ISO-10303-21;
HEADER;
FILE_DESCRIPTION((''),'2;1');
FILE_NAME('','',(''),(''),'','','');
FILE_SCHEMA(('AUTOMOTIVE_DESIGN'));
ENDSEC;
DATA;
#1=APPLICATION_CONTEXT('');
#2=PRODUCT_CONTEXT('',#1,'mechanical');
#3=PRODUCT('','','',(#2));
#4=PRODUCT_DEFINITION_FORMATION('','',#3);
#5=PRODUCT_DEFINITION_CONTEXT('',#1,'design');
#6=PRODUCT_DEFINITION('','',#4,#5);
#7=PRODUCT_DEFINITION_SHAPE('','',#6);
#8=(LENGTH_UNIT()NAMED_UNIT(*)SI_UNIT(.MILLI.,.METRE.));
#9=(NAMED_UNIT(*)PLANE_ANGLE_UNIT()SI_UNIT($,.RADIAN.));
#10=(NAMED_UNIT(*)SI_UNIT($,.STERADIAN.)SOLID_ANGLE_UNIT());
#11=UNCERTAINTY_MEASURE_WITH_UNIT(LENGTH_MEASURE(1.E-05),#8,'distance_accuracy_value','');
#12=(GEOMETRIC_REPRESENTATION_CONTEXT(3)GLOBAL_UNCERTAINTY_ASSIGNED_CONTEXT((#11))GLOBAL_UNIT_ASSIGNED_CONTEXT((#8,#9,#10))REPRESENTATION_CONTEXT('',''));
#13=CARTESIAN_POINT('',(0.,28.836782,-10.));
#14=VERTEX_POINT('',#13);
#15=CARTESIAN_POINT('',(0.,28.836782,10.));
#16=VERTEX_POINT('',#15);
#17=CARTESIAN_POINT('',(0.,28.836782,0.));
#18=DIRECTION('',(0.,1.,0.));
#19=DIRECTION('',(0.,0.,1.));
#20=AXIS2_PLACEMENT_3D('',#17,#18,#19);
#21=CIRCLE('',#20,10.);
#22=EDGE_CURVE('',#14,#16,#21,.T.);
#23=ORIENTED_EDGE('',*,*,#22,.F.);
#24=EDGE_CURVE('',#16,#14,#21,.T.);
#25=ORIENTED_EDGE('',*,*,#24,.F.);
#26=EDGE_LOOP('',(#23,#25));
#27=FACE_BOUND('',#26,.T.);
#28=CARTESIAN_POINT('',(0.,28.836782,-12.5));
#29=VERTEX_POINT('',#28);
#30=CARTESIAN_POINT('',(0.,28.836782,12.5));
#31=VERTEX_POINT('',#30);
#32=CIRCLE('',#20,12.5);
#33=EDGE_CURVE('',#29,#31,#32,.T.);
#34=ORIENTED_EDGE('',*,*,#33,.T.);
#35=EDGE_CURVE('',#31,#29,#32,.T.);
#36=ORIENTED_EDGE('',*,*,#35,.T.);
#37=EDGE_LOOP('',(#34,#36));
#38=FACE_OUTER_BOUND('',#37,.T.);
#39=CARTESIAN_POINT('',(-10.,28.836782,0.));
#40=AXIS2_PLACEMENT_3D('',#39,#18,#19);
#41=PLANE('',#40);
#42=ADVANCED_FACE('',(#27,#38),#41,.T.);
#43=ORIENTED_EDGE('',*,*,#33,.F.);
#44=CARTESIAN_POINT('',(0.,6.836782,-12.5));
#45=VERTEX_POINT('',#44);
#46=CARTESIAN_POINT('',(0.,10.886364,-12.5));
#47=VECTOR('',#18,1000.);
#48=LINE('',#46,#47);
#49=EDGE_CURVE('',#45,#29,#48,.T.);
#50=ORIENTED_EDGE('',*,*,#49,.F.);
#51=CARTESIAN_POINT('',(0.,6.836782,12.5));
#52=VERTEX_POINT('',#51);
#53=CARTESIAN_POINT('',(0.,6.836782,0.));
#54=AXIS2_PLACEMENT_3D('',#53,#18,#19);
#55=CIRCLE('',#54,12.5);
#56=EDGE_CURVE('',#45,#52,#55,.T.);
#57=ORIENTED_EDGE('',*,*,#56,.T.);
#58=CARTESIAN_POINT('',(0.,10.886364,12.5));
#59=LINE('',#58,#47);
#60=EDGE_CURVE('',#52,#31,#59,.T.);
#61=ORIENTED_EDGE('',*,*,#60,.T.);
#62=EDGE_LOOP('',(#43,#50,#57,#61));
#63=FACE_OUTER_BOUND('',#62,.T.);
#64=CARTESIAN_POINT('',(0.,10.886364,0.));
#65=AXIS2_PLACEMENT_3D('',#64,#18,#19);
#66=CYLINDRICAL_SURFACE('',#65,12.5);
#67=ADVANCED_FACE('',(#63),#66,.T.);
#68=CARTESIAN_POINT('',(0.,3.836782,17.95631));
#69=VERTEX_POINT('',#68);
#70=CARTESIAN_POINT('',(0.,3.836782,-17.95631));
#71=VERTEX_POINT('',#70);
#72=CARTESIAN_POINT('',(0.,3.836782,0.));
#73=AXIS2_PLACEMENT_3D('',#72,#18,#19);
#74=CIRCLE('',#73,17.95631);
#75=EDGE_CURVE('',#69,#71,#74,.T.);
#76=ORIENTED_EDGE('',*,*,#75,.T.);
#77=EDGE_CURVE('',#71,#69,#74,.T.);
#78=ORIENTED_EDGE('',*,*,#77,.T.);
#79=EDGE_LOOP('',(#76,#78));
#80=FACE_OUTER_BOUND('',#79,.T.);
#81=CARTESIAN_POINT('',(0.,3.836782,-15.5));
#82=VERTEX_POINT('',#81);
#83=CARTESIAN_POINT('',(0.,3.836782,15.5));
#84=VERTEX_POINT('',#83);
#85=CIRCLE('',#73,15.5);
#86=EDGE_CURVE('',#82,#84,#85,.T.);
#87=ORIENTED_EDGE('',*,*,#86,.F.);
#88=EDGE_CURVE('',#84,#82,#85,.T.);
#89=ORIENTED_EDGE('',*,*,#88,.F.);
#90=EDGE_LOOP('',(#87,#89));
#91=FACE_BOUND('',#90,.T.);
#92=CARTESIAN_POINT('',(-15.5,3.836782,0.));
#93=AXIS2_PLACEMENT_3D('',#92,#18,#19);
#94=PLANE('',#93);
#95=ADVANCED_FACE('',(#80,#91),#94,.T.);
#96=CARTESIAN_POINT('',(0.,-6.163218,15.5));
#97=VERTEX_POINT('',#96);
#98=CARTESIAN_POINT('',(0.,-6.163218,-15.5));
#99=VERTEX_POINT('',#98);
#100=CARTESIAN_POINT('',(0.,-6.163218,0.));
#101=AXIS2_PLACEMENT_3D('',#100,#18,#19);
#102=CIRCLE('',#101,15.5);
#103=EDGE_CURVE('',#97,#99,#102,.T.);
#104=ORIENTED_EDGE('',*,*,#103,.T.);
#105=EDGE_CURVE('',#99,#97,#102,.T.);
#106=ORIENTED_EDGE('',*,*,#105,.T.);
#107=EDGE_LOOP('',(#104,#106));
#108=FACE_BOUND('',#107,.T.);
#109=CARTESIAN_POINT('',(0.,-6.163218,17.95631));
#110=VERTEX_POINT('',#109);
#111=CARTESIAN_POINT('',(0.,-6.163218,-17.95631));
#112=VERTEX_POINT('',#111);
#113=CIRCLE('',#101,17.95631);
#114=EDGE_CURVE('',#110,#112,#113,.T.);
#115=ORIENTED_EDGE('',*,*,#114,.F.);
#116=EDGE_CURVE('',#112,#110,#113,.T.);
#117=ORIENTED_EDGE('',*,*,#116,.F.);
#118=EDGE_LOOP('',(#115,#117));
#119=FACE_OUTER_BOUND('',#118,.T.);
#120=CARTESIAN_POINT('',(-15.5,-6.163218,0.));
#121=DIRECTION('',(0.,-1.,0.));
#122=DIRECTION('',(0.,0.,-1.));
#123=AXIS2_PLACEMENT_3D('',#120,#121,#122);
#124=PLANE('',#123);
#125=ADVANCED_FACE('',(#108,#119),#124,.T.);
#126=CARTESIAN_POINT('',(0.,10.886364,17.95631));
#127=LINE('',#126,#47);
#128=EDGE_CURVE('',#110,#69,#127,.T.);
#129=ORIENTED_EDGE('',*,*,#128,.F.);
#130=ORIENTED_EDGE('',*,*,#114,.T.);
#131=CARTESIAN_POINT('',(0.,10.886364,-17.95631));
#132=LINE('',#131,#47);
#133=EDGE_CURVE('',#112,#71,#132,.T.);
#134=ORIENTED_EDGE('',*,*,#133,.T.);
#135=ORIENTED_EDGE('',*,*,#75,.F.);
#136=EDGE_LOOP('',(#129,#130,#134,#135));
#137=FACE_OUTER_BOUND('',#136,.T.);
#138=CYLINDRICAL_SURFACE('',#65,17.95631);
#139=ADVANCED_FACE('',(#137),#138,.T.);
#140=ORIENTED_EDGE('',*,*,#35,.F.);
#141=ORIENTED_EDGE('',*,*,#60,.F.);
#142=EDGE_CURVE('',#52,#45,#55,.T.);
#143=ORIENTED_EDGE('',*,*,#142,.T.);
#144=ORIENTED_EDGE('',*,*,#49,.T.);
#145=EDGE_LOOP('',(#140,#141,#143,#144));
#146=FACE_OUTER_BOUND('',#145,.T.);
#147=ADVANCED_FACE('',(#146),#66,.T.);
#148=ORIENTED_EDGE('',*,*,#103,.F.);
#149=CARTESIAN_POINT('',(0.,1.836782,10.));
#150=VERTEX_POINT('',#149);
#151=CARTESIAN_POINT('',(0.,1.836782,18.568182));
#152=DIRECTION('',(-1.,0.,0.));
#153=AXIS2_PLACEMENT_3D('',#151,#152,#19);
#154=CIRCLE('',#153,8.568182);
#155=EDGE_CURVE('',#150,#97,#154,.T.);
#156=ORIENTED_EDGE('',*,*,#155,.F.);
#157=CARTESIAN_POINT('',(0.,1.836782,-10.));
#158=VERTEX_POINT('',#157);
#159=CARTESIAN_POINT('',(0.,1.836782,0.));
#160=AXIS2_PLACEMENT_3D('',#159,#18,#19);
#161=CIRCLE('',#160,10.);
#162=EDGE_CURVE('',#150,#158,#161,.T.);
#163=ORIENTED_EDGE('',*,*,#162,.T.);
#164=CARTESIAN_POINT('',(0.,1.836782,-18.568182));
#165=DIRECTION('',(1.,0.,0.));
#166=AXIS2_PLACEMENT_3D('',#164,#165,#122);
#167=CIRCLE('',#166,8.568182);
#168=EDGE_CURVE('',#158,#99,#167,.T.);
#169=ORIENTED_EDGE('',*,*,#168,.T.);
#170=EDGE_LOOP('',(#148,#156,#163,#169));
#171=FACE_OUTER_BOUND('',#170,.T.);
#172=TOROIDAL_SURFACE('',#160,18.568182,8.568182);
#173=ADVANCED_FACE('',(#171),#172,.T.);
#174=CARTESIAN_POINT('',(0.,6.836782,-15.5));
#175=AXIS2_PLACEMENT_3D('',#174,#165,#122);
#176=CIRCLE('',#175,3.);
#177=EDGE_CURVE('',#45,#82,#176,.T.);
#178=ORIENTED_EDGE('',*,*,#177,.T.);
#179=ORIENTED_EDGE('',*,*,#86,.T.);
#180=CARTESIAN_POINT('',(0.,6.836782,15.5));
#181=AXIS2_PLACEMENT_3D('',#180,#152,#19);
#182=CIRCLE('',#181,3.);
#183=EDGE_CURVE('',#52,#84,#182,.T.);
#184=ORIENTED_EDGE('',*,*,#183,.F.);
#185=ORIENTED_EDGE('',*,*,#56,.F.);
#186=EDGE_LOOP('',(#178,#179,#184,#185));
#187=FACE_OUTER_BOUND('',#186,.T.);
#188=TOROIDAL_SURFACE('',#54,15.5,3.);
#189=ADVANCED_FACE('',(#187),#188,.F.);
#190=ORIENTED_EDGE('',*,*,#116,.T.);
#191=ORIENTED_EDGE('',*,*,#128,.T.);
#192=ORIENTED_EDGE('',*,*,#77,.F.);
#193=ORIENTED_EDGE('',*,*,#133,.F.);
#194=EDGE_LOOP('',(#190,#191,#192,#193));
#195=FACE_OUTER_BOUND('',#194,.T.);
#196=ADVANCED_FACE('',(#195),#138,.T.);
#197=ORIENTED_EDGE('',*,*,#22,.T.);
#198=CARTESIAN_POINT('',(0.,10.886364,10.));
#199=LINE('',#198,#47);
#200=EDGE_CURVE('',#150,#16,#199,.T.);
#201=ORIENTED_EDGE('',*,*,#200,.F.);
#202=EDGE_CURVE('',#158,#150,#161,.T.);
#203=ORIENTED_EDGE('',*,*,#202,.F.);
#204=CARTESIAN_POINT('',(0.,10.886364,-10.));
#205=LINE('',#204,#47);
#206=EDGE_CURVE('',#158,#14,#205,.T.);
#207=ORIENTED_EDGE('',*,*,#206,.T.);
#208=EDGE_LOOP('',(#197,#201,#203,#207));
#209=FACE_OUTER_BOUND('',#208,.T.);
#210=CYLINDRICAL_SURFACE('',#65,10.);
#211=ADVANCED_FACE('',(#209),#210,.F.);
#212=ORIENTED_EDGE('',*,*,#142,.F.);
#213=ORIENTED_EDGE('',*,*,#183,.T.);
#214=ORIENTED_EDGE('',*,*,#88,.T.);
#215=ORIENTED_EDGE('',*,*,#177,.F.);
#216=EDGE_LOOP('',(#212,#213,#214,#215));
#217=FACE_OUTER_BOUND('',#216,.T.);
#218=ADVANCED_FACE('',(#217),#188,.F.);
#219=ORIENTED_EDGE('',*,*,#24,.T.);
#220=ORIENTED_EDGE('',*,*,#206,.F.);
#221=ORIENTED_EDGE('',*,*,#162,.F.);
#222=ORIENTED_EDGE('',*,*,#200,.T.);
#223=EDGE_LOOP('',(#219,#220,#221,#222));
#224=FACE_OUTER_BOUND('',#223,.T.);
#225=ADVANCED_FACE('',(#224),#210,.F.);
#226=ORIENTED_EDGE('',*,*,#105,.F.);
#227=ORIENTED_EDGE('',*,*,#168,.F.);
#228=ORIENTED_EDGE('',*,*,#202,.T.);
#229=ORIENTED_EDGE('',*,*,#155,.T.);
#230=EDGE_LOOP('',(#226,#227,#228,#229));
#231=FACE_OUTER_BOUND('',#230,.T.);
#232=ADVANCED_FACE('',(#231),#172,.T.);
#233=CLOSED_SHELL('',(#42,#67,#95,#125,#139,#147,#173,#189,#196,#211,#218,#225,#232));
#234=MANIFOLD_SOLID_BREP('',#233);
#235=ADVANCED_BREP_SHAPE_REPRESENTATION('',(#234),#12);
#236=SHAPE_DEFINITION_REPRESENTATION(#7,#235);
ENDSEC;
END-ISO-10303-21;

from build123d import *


with BuildPart() as part:
    # Sketch1 → Revolve2 (revolve)
    with BuildSketch(Plane.XY, mode=Mode.PRIVATE) as revolve2_sk:
        with BuildLine():
            Line((-10, 28.836781592), (-12.5, 28.836781592))
            Line((-12.5, 28.836781592), (-12.5, 6.836781592))
            ThreePointArc((-12.5, 6.836781592), (-13.378679656, 4.715461249), (-15.5, 3.836781592))
            Line((-15.5, 3.836781592), (-17.956309532, 3.836781592))
            Line((-17.956309532, 3.836781592), (-17.956309532, -6.163218408))
            Line((-17.956309532, -6.163218408), (-15.5, -6.163218408))
            ThreePointArc((-15.5, -6.163218408), (-11.507640786, -3.017340367), (-10, 1.836781592))
            Line((-10, 1.836781592), (-10, 28.836781592))
        make_face()
    revolve(revolve2_sk.sketch.rotate(Axis((0, 10.886363636, 0), (0, -1, 0)), 270), axis=Axis((0, 10.886363636, 0), (0, -1, 0)))


solid = part.part
